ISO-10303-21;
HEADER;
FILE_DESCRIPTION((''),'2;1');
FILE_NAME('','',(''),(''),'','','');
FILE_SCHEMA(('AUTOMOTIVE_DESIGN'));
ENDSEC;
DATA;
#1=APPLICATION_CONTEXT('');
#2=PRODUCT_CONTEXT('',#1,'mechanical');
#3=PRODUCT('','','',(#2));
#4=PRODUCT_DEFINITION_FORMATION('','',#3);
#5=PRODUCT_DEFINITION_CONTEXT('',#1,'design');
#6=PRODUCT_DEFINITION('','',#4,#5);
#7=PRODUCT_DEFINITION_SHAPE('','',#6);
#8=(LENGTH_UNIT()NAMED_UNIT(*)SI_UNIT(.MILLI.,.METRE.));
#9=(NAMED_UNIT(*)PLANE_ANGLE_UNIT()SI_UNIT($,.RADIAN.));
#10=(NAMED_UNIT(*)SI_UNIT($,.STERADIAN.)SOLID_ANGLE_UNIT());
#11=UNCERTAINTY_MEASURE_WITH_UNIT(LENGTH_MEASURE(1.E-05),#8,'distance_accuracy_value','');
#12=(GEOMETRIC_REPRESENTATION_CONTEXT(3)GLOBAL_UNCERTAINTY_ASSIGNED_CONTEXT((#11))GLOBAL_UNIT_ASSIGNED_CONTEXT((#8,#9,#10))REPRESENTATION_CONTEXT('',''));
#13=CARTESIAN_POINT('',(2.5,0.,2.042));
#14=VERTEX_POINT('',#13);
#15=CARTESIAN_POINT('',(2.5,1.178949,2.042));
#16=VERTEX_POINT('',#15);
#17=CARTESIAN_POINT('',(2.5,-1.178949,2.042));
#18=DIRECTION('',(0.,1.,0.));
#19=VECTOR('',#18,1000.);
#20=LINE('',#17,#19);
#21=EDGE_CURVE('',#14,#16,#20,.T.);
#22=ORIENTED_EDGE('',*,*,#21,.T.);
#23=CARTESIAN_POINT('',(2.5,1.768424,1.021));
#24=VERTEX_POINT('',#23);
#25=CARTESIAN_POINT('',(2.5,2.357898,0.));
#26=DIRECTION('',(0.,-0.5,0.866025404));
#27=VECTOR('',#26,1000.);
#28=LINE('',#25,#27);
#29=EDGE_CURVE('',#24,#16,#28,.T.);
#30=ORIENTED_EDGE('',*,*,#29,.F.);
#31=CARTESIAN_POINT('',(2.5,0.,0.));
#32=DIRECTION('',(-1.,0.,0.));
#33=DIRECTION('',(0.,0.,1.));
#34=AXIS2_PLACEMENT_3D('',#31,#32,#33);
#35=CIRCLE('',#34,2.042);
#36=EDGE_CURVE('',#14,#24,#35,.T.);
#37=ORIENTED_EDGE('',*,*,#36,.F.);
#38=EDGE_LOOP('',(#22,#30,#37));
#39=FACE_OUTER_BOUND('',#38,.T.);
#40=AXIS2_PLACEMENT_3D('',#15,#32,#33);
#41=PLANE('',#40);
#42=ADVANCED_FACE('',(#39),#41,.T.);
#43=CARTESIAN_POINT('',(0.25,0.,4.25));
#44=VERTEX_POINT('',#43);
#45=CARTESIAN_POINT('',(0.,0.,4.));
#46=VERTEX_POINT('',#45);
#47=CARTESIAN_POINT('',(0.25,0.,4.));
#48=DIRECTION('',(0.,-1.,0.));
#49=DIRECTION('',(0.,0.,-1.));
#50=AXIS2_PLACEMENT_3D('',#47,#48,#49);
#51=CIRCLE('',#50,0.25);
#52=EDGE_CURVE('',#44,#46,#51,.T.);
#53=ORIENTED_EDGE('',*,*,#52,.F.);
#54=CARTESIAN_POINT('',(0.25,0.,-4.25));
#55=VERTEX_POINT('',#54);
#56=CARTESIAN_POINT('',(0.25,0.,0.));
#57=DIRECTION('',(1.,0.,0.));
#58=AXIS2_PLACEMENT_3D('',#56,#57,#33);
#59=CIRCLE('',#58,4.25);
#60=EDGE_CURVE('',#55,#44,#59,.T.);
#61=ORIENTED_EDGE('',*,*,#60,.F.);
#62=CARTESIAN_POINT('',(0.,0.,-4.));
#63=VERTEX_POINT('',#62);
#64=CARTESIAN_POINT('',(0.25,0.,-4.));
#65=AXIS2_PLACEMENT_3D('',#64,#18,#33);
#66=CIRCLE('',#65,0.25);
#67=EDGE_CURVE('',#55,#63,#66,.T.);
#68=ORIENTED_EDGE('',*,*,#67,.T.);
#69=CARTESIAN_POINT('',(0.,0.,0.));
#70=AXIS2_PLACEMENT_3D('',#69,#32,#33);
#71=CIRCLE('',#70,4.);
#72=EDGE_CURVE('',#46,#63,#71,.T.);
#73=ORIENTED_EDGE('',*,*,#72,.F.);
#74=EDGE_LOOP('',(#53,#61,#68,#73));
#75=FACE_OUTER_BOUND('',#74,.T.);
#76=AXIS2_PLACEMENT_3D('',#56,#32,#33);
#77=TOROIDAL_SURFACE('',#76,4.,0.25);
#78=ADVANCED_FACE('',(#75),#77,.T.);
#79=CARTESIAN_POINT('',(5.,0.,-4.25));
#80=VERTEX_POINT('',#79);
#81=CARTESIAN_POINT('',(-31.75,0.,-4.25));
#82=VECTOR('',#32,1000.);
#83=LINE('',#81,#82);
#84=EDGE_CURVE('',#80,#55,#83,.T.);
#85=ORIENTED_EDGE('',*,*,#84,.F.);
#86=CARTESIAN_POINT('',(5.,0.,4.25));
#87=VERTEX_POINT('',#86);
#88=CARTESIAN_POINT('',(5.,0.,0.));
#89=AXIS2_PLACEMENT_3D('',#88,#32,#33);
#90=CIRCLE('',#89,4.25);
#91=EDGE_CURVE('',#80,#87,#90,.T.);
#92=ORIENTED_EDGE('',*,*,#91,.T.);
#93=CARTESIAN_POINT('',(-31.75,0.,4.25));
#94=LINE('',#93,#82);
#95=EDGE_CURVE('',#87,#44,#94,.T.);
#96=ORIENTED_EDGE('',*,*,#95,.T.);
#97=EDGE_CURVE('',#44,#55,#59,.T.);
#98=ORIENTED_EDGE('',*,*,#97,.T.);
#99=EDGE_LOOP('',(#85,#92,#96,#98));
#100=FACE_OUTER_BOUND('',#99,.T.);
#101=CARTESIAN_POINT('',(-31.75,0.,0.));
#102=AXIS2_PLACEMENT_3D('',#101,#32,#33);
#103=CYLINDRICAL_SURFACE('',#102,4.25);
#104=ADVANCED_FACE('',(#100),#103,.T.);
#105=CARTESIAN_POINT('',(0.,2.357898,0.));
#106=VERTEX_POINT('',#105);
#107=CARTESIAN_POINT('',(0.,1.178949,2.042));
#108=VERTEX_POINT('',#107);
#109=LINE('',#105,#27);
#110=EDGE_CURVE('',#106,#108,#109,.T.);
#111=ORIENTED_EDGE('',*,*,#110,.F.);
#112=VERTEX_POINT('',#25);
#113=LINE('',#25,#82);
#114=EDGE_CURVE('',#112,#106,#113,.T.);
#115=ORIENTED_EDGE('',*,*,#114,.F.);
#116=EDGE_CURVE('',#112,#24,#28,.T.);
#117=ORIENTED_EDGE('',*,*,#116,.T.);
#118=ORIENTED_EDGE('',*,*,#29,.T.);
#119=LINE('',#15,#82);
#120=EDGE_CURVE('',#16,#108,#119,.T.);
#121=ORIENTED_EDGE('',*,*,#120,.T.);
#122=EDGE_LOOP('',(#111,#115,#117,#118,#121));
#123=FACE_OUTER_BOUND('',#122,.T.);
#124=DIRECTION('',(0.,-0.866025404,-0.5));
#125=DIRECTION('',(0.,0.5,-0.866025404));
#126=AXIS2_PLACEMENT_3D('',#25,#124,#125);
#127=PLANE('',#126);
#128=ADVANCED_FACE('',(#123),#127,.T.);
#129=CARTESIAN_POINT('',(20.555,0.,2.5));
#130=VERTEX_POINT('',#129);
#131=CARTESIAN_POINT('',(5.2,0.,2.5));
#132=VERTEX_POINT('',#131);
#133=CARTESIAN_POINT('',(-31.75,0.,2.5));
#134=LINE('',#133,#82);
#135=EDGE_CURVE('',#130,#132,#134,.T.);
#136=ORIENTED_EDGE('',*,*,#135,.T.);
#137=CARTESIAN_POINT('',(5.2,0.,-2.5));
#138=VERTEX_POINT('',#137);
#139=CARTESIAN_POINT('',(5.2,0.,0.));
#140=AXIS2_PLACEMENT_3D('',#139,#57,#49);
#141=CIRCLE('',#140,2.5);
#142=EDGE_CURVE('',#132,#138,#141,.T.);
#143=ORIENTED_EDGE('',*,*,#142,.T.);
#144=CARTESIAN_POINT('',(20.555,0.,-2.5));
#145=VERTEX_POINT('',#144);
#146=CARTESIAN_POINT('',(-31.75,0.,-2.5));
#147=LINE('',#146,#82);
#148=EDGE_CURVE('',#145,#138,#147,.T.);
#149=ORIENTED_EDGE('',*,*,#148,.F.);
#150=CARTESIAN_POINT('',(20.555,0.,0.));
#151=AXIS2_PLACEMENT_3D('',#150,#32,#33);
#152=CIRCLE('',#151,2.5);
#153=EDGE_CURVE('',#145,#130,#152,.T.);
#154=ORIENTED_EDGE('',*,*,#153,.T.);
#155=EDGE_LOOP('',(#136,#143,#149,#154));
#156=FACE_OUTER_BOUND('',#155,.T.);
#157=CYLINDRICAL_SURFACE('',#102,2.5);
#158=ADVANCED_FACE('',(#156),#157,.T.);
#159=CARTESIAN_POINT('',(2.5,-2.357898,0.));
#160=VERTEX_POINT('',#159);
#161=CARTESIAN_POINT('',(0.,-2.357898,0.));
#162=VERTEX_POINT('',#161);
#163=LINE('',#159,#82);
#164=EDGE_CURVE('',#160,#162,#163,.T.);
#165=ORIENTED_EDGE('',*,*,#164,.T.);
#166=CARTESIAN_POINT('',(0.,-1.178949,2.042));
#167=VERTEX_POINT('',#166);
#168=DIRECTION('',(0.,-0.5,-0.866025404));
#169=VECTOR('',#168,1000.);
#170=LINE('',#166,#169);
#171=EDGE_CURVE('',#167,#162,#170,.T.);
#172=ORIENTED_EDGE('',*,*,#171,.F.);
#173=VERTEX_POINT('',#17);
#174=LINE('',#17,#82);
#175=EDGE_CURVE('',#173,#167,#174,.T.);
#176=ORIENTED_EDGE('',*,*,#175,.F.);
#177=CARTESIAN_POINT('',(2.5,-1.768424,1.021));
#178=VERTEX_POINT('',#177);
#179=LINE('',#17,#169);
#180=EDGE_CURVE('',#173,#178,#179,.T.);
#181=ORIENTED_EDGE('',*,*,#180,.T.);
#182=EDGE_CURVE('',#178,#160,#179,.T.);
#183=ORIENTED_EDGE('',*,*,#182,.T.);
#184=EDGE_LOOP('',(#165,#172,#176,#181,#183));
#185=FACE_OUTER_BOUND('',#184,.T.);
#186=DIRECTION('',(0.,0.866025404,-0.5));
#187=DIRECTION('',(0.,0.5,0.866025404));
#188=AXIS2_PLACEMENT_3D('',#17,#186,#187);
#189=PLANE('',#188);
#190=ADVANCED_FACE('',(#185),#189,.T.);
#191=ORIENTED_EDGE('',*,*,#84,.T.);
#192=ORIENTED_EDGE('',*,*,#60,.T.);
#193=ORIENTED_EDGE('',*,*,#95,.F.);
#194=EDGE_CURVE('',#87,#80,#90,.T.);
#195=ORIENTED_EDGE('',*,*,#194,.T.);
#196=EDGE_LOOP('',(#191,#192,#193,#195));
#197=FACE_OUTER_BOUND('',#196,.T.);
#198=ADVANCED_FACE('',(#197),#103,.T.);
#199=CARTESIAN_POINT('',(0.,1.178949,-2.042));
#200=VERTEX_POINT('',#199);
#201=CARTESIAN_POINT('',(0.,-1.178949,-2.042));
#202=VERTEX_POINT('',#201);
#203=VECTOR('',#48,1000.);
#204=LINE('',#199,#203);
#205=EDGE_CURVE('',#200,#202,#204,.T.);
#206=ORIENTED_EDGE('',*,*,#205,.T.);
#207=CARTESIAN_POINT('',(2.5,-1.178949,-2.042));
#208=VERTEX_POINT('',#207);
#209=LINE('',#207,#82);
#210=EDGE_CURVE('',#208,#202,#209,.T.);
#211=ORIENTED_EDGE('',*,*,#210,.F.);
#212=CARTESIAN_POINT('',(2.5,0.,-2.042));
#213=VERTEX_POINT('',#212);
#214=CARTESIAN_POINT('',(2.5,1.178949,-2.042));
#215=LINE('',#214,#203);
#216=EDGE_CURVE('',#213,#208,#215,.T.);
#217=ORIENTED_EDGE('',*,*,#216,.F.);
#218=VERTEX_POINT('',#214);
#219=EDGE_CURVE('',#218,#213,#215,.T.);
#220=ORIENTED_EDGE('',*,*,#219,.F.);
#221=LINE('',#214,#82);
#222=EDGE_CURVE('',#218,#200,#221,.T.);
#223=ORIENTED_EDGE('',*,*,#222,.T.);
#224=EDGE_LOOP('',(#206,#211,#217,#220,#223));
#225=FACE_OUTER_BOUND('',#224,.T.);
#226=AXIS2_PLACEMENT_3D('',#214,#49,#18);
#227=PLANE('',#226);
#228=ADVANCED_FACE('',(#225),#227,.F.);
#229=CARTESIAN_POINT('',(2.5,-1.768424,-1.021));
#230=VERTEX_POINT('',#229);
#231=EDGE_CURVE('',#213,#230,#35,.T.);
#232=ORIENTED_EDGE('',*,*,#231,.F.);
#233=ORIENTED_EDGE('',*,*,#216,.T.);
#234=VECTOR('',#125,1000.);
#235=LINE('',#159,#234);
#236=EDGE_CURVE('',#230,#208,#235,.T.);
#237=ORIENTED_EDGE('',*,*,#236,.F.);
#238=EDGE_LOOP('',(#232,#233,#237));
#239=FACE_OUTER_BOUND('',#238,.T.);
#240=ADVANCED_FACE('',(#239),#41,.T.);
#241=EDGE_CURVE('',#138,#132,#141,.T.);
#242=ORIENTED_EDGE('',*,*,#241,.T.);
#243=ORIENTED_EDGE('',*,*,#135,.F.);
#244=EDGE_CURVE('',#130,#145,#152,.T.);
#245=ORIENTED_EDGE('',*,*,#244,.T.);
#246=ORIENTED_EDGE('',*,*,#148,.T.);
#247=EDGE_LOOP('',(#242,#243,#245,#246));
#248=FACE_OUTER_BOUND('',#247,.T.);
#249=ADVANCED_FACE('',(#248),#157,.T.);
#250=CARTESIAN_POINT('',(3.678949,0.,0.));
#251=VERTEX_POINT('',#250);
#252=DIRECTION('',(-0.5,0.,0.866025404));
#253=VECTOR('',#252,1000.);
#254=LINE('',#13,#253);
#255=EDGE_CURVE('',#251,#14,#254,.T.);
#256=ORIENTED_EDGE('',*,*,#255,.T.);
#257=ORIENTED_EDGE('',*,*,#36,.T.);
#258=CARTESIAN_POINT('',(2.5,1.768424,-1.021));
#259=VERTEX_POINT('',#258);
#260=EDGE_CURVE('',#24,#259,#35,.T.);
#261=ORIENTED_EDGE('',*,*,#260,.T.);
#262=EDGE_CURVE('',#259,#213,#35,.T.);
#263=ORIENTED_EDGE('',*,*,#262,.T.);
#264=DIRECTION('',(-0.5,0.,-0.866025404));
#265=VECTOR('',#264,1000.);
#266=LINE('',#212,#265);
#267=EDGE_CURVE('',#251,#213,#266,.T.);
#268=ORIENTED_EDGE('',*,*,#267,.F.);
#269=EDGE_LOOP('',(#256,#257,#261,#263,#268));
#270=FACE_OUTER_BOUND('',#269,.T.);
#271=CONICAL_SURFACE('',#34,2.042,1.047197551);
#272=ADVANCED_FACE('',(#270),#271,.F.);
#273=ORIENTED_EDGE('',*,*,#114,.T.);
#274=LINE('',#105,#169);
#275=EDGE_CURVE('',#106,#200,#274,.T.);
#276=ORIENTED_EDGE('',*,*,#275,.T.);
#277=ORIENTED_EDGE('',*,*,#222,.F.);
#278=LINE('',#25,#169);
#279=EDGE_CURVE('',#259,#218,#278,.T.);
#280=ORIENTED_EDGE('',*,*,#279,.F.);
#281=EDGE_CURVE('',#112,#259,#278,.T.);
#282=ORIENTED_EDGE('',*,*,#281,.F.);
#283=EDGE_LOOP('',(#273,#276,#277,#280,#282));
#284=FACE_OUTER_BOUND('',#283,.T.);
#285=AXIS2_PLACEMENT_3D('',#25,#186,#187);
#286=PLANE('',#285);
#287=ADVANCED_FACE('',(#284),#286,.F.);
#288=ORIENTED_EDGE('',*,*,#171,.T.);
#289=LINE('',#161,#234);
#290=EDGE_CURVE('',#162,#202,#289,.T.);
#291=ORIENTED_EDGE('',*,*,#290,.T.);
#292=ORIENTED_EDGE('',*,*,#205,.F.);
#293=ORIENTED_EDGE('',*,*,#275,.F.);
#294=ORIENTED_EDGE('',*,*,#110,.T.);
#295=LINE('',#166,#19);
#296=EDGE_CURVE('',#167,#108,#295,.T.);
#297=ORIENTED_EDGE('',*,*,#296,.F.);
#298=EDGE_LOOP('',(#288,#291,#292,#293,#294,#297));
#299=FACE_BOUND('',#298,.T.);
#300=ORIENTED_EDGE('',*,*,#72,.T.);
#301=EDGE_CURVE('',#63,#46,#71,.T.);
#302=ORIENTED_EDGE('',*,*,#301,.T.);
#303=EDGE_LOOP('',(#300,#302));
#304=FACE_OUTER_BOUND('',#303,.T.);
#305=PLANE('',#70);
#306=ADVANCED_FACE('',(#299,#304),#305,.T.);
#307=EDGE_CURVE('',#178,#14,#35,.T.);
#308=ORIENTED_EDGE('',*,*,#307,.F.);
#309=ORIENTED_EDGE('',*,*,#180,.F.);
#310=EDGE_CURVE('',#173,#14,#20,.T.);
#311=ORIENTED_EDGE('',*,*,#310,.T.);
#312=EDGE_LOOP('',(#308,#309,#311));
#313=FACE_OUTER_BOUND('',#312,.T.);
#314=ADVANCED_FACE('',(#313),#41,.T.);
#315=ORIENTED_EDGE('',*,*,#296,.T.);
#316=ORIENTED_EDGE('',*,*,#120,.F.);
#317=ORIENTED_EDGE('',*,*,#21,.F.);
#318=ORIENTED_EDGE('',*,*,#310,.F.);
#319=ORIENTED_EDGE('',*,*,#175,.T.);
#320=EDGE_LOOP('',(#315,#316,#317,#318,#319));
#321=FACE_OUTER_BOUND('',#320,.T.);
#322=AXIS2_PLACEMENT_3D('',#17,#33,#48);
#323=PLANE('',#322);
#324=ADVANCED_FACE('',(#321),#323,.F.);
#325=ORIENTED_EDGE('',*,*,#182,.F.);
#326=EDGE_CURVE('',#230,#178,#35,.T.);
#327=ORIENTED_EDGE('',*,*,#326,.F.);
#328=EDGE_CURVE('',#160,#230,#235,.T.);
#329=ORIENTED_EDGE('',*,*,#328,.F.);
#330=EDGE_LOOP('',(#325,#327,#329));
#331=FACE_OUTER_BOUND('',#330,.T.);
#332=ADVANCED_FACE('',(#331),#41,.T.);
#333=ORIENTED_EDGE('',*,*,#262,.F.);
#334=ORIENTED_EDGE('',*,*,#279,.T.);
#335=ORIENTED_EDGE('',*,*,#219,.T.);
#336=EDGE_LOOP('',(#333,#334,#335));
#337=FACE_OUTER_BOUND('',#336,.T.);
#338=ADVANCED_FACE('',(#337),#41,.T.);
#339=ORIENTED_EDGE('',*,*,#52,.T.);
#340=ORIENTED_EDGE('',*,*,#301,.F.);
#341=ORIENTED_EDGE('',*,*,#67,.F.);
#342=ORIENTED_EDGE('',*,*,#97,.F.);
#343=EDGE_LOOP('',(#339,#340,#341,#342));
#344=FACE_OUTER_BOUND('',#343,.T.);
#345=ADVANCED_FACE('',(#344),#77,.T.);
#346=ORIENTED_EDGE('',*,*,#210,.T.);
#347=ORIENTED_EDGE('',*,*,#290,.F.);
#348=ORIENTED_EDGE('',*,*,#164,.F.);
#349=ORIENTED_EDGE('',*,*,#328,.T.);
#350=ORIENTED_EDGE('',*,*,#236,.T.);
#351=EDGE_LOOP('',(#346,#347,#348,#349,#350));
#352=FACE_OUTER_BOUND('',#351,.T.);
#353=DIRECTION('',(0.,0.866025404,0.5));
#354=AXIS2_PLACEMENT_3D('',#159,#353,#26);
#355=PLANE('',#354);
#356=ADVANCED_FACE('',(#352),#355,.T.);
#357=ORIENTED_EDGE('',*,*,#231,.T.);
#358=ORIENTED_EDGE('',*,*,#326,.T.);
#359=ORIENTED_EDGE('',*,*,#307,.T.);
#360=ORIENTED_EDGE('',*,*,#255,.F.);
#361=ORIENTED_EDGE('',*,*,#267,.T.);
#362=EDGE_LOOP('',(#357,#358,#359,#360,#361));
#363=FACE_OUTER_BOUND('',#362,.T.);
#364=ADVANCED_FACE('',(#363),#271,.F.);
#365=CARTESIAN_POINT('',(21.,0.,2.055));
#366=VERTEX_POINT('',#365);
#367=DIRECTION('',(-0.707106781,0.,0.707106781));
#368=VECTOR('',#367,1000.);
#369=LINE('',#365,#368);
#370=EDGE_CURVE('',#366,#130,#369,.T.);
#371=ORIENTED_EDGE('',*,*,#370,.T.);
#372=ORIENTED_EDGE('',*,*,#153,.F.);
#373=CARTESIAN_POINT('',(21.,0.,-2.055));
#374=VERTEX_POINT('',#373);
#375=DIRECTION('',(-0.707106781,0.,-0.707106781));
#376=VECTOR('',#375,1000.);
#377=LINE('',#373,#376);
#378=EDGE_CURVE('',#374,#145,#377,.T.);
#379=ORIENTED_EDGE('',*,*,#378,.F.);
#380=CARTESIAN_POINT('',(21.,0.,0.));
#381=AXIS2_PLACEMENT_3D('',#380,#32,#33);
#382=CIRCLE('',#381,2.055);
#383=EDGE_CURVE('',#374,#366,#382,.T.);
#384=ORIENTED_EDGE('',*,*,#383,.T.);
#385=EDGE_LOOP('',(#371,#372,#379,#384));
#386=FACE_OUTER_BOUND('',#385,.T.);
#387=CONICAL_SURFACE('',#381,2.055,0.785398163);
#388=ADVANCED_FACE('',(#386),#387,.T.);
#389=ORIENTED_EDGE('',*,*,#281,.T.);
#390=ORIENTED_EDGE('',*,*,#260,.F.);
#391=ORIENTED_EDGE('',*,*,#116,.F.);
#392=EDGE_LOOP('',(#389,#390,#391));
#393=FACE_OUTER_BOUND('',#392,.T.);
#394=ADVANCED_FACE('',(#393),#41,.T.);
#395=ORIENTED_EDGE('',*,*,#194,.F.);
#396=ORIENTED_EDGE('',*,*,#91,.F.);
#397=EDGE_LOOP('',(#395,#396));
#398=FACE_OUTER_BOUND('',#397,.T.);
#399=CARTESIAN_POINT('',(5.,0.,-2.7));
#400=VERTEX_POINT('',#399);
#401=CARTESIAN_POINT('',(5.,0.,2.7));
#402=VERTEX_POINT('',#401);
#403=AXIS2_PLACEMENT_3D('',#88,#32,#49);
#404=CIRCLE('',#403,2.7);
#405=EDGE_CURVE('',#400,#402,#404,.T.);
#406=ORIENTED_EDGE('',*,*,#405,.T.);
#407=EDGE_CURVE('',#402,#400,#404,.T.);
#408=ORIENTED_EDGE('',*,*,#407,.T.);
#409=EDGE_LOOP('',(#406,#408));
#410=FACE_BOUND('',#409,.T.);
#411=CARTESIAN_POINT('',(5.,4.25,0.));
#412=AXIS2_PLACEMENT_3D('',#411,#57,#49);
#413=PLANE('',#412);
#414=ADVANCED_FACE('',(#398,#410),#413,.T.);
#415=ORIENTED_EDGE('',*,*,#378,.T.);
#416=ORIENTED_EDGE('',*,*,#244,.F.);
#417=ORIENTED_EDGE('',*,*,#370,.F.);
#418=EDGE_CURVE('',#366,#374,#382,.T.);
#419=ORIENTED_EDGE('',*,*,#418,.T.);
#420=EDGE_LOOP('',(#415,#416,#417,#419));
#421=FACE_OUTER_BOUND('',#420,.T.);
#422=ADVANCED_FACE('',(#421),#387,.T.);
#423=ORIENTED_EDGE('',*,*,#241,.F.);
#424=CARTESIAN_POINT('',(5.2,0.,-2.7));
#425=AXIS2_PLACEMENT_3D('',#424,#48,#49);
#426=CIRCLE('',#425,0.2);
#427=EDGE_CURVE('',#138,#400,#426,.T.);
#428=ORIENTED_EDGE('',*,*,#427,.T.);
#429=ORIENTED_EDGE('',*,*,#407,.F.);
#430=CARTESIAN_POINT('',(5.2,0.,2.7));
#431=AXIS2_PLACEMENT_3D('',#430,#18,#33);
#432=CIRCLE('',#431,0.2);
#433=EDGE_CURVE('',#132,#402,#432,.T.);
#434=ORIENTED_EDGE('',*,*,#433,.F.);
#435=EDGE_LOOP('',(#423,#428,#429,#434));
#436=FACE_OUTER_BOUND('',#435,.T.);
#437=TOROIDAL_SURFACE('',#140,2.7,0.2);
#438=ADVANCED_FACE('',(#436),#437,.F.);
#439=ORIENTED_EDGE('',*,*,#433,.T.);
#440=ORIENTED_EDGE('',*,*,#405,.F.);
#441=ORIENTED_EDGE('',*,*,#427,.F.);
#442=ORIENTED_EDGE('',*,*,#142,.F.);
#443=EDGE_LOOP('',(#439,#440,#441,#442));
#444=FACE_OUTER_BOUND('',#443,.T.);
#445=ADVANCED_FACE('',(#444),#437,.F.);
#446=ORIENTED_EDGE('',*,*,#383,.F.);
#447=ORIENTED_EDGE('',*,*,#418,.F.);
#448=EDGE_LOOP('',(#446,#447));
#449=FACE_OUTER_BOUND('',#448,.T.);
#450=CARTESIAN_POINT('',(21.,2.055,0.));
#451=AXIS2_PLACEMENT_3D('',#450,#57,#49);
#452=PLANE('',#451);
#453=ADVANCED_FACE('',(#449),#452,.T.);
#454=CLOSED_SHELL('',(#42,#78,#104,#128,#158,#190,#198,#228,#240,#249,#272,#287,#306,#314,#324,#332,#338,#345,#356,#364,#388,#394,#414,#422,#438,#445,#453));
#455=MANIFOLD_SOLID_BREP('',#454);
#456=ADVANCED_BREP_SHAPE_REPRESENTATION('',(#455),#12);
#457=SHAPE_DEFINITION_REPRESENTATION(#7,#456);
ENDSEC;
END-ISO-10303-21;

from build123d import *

# Parameters (mm, degrees)
FILLET1_R   = 0.2
FILLET2_R   = 0.25
HEX_2_DEPTH = 2.5


with BuildPart() as part:
    # BodySke → Base-Revolve (revolve)
    with BuildSketch(Plane.XY, mode=Mode.PRIVATE) as base_revolve_sk:
        Polygon((0, 0), (0, 4.25), (5, 4.25), (5, 2.5), (20.555, 2.5), (21, 2.055), (21, 0), align=None)
    revolve(base_revolve_sk.sketch.rotate(Axis((-31.75, 0, 0), (1, 0, 0)), 90), axis=Axis((-31.75, 0, 0), (1, 0, 0)))

    # Fillet1
    fillet1_edges = [part.edges().sort_by_distance(p)[0] for p in [
        (5, 0, -2.5),
    ]]
    fillet(fillet1_edges, radius=FILLET1_R)

    # Fillet2
    fillet2_edges = [part.edges().sort_by_distance(p)[0] for p in [
        (0, 0, -4.25),
    ]]
    fillet(fillet2_edges, radius=FILLET2_R)

    # Sketch2 → Hex-PreBroach (revolve, cut)
    with BuildSketch(Plane.XY, mode=Mode.PRIVATE) as hex_prebroach_sk:
        Polygon((0, 2.042), (2.5, 2.042), (3.67894925, 0), (0, 0), align=None)
    revolve(hex_prebroach_sk.sketch.rotate(Axis((0, 0, 0), (1, 0, 0)), 90), axis=Axis((0, 0, 0), (1, 0, 0)), mode=Mode.SUBTRACT)

    # Sketch3 → Hex 2 (cut)
    with BuildSketch(Plane(origin=(0, 0, 0), x_dir=(0, 0.500000000000001, 0.866025403784438), z_dir=(-1, 0, 0))):
        Polygon((1.17894925, 2.042), (-1.17894925, 2.042), (-2.357898499, 0), (-1.17894925, -2.042), (1.17894925, -2.042), (2.357898499, 0), align=None)
    extrude(amount=-HEX_2_DEPTH, mode=Mode.SUBTRACT)


solid = part.part
